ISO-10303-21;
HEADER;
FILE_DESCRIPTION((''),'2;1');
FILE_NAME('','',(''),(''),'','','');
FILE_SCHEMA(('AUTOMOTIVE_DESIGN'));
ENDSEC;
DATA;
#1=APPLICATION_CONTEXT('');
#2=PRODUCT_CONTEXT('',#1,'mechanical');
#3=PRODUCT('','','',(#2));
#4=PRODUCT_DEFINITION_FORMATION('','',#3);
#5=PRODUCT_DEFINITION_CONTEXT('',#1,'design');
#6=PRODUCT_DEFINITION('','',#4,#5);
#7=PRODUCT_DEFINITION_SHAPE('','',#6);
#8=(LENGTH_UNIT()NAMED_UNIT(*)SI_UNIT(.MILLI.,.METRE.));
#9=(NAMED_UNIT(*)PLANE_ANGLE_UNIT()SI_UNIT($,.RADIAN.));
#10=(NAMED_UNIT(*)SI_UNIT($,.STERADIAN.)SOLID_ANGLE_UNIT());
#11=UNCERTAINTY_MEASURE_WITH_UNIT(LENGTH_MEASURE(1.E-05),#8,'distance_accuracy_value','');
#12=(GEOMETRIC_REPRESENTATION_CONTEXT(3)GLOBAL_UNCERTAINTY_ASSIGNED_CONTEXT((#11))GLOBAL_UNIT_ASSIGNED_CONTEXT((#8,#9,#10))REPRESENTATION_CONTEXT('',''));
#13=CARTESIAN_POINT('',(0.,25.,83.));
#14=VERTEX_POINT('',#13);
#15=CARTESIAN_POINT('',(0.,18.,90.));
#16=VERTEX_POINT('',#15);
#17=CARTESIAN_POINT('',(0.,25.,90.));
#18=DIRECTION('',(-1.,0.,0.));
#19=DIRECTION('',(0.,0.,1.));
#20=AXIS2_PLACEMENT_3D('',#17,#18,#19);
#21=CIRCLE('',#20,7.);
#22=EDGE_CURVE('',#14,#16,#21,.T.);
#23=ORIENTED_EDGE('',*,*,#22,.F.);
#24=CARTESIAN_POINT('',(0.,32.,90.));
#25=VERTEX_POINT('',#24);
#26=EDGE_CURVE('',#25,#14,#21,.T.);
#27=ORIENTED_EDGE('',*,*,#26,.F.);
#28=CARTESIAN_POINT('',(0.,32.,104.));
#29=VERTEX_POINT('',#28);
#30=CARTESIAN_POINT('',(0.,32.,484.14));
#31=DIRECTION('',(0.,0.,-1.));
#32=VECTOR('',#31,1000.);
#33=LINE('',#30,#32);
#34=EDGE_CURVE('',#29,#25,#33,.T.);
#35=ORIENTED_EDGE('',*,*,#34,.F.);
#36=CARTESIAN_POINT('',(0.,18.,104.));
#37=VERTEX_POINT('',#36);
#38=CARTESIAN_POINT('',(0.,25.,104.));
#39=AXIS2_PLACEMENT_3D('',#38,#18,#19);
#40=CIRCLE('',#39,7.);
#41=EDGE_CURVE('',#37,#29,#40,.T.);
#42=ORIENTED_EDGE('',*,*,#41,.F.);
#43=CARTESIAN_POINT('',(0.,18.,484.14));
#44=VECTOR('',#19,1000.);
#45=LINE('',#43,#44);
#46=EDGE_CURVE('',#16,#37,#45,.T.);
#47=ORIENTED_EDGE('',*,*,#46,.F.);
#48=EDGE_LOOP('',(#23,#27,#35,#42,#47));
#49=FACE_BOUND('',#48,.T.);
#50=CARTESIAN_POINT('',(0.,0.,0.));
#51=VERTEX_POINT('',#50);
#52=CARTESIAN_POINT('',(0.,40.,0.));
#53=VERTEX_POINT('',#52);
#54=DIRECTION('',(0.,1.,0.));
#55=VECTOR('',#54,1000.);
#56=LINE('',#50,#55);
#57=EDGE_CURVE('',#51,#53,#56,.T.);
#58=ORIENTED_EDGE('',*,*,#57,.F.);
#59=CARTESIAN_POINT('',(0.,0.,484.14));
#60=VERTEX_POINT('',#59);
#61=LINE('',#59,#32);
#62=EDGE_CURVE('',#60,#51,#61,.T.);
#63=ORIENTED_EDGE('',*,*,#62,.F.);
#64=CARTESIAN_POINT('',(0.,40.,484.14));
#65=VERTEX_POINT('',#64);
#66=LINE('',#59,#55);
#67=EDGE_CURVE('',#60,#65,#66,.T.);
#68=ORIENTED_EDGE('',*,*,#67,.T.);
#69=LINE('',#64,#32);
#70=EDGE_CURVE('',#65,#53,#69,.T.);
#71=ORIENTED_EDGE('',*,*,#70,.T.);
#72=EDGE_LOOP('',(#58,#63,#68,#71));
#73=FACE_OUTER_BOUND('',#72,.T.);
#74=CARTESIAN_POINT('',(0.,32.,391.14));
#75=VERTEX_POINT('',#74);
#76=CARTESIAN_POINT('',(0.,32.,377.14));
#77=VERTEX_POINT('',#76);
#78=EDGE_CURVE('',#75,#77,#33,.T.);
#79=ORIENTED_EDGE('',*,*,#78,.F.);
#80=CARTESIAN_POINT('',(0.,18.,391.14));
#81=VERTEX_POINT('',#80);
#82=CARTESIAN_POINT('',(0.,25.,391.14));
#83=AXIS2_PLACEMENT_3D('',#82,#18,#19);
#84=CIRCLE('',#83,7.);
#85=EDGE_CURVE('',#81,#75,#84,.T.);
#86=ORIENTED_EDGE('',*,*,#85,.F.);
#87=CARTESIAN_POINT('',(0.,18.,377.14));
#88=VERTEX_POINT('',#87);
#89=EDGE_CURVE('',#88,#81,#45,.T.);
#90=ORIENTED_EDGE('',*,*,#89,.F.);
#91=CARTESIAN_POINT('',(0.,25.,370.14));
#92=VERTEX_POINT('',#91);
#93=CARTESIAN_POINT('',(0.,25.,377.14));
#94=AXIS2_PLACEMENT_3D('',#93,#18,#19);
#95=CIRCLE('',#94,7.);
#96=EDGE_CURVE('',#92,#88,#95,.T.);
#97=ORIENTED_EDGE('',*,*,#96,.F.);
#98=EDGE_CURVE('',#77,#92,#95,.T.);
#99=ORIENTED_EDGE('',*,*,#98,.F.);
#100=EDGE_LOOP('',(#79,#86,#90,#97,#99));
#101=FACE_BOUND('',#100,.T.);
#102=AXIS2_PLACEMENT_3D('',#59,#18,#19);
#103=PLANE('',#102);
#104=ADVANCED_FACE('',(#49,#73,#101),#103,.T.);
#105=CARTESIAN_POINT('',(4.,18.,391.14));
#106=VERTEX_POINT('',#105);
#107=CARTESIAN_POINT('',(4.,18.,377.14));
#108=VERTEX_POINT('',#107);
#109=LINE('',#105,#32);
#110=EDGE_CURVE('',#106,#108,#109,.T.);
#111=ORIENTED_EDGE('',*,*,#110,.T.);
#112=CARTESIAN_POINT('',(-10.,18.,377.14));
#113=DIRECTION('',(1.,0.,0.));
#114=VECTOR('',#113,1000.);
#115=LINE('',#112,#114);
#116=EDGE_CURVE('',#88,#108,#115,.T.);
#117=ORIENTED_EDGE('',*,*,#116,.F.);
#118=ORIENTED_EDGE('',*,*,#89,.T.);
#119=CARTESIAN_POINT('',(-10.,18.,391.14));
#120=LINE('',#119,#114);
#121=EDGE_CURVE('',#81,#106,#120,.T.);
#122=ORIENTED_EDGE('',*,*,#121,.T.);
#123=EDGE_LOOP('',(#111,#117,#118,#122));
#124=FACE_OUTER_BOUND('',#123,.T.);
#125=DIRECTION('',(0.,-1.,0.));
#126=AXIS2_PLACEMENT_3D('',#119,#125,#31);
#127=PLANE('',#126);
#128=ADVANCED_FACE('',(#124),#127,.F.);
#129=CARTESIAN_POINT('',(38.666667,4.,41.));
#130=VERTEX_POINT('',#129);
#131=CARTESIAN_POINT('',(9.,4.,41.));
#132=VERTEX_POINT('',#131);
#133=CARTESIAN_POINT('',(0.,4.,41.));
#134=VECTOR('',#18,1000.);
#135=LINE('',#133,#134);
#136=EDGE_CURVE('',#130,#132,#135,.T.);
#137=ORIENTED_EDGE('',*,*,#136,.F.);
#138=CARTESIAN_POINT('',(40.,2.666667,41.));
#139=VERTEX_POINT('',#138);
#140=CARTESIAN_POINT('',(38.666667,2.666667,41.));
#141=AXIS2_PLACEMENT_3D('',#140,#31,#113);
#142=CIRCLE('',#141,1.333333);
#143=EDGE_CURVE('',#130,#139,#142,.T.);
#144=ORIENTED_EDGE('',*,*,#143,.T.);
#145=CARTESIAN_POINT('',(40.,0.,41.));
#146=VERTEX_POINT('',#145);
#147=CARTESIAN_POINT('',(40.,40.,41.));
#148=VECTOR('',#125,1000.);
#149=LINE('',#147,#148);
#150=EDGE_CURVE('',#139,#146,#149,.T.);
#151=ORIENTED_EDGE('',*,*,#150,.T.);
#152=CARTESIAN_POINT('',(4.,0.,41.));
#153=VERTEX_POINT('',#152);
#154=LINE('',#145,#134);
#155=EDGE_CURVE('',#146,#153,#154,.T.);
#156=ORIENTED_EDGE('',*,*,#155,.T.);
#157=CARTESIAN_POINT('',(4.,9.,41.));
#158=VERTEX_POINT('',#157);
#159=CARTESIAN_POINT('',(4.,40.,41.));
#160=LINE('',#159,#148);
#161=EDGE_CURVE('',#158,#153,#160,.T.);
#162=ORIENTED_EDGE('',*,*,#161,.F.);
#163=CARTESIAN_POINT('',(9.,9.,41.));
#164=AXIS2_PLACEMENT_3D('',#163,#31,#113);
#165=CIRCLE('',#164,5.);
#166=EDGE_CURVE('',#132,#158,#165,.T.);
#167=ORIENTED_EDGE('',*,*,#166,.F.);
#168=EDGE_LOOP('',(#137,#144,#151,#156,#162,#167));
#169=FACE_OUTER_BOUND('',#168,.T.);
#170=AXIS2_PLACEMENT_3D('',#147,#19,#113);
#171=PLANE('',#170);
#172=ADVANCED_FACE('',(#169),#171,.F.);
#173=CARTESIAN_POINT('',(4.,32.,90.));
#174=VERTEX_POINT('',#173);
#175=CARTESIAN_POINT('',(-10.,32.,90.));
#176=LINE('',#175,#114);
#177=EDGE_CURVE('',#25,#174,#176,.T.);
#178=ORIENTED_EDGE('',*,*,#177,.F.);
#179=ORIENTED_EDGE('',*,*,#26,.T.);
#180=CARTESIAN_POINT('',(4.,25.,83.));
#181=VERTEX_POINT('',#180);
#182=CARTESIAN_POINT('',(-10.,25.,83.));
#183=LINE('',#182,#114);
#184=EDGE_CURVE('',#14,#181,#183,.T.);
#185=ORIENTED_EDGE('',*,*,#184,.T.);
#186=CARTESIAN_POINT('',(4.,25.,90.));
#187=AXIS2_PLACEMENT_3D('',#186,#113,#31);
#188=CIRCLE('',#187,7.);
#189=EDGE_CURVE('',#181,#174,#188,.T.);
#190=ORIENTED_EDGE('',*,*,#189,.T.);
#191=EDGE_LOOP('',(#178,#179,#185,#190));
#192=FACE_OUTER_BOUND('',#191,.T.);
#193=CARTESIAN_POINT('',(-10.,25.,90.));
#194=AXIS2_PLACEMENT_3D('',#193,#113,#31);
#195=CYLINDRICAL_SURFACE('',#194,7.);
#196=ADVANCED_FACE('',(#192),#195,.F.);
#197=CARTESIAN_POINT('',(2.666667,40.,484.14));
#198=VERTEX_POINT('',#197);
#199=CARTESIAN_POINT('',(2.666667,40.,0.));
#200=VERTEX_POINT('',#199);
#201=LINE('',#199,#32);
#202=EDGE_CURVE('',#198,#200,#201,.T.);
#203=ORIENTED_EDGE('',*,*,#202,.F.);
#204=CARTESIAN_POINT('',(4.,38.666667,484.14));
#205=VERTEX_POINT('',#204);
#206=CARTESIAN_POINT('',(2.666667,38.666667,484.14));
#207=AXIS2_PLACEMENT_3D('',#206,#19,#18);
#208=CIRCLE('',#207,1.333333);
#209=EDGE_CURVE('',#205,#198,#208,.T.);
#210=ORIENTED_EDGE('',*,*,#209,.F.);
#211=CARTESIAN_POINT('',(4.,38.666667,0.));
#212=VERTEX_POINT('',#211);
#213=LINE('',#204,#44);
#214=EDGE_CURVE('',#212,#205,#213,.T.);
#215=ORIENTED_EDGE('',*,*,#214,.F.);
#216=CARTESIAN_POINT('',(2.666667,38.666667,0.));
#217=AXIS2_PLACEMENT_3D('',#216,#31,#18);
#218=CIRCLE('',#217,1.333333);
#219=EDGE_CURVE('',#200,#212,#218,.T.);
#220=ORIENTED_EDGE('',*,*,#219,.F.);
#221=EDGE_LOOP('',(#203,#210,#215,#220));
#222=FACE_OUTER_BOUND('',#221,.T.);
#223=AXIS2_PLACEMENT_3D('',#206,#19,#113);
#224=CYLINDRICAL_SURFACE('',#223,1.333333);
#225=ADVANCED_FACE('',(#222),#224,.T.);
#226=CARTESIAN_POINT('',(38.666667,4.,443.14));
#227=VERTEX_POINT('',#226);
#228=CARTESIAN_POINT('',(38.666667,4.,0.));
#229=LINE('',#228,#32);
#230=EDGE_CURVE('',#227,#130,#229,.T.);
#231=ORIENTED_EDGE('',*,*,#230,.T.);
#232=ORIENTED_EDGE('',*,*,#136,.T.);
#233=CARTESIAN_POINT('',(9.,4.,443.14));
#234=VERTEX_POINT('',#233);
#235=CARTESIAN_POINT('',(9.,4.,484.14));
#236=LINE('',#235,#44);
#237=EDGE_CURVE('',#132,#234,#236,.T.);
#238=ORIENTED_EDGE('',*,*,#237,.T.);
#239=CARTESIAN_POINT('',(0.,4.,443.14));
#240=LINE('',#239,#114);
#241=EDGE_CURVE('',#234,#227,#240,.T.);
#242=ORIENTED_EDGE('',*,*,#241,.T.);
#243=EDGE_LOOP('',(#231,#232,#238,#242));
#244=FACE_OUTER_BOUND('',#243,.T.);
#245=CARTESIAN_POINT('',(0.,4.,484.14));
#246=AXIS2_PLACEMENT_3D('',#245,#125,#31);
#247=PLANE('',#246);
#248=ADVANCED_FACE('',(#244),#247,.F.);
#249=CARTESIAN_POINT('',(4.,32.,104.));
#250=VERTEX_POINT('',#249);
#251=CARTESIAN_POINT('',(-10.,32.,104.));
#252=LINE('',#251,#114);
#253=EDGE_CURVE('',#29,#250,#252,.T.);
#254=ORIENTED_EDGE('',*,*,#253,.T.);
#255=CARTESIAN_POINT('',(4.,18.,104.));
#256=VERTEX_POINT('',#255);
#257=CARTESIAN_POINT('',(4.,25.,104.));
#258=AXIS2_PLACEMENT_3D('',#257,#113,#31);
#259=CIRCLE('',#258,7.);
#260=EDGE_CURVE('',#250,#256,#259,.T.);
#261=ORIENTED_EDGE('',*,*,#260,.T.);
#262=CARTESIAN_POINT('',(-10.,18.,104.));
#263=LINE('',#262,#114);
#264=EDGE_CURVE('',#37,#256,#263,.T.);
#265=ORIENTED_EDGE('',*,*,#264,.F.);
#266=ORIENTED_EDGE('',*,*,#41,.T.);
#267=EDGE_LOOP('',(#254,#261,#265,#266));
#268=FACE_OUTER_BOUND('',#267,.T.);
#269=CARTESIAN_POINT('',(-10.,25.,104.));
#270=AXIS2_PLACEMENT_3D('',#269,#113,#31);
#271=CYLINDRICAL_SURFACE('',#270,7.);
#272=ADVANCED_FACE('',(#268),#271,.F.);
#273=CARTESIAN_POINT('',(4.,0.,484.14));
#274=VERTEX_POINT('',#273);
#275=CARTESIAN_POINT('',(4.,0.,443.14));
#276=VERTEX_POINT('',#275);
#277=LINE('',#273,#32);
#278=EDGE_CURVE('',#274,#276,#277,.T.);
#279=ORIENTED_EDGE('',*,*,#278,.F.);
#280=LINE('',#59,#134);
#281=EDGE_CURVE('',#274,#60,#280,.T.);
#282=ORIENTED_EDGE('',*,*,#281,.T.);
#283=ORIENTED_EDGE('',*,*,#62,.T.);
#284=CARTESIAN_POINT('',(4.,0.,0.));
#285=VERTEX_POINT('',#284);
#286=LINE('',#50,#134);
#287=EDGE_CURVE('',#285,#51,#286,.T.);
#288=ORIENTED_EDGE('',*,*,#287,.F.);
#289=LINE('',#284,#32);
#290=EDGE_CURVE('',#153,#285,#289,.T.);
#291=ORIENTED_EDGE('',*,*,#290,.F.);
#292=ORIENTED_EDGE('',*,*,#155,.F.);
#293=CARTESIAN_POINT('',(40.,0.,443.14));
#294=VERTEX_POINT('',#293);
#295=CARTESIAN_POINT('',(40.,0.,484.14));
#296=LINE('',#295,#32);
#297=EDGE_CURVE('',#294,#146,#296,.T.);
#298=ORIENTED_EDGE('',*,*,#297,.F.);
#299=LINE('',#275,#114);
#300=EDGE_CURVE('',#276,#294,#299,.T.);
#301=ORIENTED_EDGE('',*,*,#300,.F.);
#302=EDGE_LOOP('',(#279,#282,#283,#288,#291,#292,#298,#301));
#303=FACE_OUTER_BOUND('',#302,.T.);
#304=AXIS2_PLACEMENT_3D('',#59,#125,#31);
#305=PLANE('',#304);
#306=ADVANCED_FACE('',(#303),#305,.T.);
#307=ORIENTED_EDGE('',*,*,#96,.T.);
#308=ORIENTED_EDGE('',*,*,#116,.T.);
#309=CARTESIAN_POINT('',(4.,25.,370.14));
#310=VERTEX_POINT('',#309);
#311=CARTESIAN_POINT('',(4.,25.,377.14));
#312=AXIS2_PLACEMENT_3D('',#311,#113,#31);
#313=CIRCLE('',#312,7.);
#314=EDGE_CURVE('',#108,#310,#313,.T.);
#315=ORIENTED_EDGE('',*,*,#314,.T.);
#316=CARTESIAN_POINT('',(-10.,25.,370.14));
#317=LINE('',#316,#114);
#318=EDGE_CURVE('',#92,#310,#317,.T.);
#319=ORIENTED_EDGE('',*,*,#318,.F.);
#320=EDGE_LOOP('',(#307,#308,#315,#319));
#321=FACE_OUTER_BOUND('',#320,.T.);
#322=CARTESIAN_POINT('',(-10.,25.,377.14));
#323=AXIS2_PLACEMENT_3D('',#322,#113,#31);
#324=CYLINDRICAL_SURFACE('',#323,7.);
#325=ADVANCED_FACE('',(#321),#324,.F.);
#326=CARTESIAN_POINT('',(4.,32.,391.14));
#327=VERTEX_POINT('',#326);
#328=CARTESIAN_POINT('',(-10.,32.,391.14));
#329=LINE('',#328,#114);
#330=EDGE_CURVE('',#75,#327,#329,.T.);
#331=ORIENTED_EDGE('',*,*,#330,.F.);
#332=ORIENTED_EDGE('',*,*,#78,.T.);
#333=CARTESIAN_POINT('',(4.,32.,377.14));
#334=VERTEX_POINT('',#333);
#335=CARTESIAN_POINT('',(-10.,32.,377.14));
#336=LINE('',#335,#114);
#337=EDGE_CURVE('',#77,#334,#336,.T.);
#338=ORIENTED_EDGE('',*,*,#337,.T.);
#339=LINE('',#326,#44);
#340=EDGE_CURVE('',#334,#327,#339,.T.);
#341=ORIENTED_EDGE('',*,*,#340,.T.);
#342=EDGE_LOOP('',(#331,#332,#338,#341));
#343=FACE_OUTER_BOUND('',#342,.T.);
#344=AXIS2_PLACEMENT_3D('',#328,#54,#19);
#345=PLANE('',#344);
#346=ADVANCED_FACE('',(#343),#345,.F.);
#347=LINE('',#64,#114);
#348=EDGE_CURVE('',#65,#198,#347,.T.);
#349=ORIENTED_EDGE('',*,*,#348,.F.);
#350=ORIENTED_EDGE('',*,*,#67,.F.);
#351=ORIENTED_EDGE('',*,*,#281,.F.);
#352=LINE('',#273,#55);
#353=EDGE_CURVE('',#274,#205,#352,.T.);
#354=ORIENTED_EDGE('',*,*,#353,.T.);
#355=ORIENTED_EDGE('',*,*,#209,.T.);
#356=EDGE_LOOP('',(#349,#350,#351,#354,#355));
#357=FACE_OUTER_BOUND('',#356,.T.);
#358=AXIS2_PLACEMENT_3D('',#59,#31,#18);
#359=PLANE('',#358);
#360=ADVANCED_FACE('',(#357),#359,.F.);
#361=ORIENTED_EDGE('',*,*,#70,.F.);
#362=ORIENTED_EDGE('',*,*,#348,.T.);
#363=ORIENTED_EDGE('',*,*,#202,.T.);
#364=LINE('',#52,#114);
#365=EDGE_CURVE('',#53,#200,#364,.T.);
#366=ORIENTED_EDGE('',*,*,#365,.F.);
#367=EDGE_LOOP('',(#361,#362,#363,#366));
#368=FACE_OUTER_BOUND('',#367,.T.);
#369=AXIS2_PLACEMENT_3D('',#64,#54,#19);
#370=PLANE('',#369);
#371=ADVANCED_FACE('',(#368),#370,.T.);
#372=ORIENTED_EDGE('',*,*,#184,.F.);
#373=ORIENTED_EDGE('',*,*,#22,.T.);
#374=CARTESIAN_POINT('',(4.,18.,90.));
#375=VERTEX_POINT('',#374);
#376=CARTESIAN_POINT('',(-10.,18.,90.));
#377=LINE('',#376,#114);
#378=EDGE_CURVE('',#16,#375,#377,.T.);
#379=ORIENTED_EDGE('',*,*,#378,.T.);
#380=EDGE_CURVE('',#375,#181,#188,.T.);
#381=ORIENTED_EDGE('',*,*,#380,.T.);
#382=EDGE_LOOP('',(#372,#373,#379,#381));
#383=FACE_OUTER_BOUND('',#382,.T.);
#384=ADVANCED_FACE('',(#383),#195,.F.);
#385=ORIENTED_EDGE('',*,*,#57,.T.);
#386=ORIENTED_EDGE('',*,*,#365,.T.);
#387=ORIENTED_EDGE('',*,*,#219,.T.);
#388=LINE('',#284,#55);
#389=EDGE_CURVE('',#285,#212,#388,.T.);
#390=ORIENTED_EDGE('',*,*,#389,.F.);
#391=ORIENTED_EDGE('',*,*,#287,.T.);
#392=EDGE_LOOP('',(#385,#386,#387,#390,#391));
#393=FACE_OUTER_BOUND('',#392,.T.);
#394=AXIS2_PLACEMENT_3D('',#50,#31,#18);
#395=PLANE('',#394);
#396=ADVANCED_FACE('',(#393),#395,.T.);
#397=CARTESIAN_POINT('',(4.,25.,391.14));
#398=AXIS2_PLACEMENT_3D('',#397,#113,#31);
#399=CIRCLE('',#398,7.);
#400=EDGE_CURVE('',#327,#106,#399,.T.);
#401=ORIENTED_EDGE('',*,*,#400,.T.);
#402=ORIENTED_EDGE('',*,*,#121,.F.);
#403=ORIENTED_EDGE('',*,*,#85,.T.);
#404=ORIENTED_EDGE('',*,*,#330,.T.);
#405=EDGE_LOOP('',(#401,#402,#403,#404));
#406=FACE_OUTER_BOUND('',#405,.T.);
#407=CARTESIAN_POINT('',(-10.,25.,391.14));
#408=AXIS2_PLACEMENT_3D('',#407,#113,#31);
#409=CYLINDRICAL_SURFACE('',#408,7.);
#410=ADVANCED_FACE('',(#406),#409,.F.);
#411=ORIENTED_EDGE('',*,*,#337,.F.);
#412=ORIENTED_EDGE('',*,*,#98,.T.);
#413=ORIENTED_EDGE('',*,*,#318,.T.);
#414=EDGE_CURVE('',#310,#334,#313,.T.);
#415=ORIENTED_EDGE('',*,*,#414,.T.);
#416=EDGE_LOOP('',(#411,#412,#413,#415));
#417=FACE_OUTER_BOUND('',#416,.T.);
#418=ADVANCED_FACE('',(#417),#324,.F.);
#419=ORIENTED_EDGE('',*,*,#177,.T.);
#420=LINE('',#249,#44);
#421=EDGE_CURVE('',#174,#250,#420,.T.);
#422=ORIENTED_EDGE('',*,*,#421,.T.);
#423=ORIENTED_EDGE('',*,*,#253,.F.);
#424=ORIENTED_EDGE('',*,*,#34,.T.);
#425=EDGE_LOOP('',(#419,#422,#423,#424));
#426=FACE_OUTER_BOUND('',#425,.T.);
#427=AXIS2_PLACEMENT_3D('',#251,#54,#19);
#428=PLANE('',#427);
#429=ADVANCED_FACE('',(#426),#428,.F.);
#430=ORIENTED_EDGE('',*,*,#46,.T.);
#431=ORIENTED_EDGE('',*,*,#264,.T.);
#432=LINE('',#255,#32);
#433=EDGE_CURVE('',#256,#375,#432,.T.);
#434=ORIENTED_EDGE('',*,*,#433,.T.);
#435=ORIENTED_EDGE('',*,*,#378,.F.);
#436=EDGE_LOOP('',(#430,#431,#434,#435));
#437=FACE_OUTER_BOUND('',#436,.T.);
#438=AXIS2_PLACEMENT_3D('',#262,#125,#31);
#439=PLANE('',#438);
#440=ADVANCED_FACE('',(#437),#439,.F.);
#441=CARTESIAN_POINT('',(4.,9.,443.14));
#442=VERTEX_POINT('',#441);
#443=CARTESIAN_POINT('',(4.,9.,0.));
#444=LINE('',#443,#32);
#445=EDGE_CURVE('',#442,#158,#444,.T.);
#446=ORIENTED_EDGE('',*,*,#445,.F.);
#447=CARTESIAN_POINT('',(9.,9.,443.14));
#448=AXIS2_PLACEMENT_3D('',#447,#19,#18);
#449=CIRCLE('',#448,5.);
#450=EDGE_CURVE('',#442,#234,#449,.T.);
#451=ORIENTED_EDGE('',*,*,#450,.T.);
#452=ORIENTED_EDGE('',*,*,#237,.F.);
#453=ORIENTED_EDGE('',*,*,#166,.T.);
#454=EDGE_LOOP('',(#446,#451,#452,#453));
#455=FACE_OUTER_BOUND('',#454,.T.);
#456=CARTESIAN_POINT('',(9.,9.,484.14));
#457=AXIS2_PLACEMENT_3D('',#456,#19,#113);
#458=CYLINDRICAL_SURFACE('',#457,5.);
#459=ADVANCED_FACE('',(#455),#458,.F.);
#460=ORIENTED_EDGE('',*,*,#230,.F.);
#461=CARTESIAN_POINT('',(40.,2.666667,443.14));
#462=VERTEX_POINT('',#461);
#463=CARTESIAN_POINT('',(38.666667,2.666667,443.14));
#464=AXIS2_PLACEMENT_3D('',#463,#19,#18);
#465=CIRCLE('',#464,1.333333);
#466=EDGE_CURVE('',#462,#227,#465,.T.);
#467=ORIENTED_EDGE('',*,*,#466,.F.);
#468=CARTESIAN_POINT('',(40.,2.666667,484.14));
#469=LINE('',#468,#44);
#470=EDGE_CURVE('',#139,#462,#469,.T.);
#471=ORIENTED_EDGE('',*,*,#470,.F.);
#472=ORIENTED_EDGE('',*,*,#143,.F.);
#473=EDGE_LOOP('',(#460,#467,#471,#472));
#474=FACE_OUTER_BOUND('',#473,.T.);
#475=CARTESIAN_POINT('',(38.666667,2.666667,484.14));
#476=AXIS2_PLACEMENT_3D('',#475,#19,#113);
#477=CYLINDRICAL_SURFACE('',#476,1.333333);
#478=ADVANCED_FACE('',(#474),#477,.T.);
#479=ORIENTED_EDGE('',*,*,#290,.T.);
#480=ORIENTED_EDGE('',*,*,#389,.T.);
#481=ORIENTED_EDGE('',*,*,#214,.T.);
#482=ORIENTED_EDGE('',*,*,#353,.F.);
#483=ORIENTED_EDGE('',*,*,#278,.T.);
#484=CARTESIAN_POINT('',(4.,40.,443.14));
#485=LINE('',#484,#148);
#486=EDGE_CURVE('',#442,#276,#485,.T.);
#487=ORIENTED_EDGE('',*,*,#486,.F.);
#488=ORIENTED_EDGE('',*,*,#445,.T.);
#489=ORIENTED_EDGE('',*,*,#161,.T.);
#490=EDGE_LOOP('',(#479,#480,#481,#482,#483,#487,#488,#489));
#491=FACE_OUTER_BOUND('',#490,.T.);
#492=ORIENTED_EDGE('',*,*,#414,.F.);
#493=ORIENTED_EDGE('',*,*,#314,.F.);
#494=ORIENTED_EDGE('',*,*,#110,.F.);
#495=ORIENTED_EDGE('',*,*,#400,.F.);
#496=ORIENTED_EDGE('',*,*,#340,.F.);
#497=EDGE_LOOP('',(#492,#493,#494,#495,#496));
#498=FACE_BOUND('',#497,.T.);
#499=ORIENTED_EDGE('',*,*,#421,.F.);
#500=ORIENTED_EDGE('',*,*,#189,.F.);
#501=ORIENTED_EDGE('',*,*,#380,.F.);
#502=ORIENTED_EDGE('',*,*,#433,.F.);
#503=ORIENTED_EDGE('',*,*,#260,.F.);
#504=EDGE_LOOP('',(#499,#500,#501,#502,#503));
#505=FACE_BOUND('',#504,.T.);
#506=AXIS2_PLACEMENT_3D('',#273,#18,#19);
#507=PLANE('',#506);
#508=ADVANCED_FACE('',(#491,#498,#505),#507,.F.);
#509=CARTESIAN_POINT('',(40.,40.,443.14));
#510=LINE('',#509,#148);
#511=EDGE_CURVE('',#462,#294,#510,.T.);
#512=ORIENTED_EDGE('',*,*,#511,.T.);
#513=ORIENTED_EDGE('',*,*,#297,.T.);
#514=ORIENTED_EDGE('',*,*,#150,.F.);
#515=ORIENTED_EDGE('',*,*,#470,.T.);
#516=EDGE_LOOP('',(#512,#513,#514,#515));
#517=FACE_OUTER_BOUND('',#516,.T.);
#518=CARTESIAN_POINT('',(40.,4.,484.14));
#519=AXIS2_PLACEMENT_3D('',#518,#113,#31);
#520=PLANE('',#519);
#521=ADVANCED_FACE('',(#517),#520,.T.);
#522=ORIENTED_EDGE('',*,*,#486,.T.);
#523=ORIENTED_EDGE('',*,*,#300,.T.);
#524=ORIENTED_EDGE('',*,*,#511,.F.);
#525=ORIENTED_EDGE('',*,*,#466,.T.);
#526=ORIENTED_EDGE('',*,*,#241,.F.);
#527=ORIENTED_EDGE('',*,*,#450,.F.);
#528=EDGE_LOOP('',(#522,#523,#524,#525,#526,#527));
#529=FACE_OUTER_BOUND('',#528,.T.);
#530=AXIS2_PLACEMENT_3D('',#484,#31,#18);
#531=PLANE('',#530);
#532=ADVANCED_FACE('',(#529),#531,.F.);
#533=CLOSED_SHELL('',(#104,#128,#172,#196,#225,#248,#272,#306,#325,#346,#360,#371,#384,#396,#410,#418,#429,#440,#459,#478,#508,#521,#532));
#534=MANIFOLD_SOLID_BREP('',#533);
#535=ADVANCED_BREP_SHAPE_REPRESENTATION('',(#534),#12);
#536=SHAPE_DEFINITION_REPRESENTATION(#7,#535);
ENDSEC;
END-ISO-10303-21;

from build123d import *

# Parameters (mm, degrees)
EXTRUDE_THIN1_DEPTH = 484.14
FILLET1_R           = 5
FILLET2_R           = 1.333333333
SKETCH2_W           = 36
SKETCH2_H           = 41
CUT_EXTRUDE1_DEPTH  = 488.43362584
SKETCH3_W           = 36
SKETCH3_H           = 41
CUT_EXTRUDE3_DEPTH  = 488.43362584
CUT_EXTRUDE4_DEPTH  = 14
LPATTERN1_COUNT     = 2
LPATTERN1_PITCH     = 287.14


with BuildPart() as part:
    # Sketch1 → Extrude-Thin1 (new body)
    with BuildSketch(Plane.XY):
        Polygon((0, 40), (0, 0), (40, 0), (40, 4), (4, 4), (4, 40), align=None)
    extrude(amount=EXTRUDE_THIN1_DEPTH)

    # Fillet1
    fillet1_edges = [part.edges().sort_by_distance(p)[0] for p in [
        (4, 4, 242.07),
    ]]
    fillet(fillet1_edges, radius=FILLET1_R)

    # Fillet2
    fillet2_edges = [part.edges().sort_by_distance(p)[0] for p in [
        (40, 4, 242.07),
        (4, 40, 242.07),
    ]]
    fillet(fillet2_edges, radius=FILLET2_R)

    # Sketch2 → Cut-Extrude1 (cut, through all)
    with BuildSketch(Plane.XZ):
        with Locations((22, 20.5)):
            Rectangle(SKETCH2_W, SKETCH2_H)
    extrude(amount=-CUT_EXTRUDE1_DEPTH, mode=Mode.SUBTRACT)

    # Sketch3 → Cut-Extrude3 (cut, through all)
    with BuildSketch(Plane.XZ):
        with Locations((22, 463.64)):
            Rectangle(SKETCH3_W, SKETCH3_H)
    extrude(amount=-CUT_EXTRUDE3_DEPTH, mode=Mode.SUBTRACT)

    # Sketch4 → Cut-Extrude4 (cut)
    with BuildSketch(Plane(origin=(4, 0, 0), x_dir=(0, 0, -1), z_dir=(1, 0, 0))):
        with BuildLine():
            Line((-391.14, 32), (-377.14, 32))
            ThreePointArc((-377.14, 32), (-370.14, 25), (-377.14, 18))
            Line((-377.14, 18), (-391.14, 18))
            ThreePointArc((-391.14, 18), (-398.14, 25), (-391.14, 32))
        make_face()
    cut_extrude4 = extrude(amount=-CUT_EXTRUDE4_DEPTH, mode=Mode.SUBTRACT)

    # LPattern1: Cut-Extrude4 ×2
    with Locations(*[(0, 0, -i * LPATTERN1_PITCH) for i in range(1, LPATTERN1_COUNT)]):
        add(cut_extrude4, mode=Mode.SUBTRACT)


solid = part.part
